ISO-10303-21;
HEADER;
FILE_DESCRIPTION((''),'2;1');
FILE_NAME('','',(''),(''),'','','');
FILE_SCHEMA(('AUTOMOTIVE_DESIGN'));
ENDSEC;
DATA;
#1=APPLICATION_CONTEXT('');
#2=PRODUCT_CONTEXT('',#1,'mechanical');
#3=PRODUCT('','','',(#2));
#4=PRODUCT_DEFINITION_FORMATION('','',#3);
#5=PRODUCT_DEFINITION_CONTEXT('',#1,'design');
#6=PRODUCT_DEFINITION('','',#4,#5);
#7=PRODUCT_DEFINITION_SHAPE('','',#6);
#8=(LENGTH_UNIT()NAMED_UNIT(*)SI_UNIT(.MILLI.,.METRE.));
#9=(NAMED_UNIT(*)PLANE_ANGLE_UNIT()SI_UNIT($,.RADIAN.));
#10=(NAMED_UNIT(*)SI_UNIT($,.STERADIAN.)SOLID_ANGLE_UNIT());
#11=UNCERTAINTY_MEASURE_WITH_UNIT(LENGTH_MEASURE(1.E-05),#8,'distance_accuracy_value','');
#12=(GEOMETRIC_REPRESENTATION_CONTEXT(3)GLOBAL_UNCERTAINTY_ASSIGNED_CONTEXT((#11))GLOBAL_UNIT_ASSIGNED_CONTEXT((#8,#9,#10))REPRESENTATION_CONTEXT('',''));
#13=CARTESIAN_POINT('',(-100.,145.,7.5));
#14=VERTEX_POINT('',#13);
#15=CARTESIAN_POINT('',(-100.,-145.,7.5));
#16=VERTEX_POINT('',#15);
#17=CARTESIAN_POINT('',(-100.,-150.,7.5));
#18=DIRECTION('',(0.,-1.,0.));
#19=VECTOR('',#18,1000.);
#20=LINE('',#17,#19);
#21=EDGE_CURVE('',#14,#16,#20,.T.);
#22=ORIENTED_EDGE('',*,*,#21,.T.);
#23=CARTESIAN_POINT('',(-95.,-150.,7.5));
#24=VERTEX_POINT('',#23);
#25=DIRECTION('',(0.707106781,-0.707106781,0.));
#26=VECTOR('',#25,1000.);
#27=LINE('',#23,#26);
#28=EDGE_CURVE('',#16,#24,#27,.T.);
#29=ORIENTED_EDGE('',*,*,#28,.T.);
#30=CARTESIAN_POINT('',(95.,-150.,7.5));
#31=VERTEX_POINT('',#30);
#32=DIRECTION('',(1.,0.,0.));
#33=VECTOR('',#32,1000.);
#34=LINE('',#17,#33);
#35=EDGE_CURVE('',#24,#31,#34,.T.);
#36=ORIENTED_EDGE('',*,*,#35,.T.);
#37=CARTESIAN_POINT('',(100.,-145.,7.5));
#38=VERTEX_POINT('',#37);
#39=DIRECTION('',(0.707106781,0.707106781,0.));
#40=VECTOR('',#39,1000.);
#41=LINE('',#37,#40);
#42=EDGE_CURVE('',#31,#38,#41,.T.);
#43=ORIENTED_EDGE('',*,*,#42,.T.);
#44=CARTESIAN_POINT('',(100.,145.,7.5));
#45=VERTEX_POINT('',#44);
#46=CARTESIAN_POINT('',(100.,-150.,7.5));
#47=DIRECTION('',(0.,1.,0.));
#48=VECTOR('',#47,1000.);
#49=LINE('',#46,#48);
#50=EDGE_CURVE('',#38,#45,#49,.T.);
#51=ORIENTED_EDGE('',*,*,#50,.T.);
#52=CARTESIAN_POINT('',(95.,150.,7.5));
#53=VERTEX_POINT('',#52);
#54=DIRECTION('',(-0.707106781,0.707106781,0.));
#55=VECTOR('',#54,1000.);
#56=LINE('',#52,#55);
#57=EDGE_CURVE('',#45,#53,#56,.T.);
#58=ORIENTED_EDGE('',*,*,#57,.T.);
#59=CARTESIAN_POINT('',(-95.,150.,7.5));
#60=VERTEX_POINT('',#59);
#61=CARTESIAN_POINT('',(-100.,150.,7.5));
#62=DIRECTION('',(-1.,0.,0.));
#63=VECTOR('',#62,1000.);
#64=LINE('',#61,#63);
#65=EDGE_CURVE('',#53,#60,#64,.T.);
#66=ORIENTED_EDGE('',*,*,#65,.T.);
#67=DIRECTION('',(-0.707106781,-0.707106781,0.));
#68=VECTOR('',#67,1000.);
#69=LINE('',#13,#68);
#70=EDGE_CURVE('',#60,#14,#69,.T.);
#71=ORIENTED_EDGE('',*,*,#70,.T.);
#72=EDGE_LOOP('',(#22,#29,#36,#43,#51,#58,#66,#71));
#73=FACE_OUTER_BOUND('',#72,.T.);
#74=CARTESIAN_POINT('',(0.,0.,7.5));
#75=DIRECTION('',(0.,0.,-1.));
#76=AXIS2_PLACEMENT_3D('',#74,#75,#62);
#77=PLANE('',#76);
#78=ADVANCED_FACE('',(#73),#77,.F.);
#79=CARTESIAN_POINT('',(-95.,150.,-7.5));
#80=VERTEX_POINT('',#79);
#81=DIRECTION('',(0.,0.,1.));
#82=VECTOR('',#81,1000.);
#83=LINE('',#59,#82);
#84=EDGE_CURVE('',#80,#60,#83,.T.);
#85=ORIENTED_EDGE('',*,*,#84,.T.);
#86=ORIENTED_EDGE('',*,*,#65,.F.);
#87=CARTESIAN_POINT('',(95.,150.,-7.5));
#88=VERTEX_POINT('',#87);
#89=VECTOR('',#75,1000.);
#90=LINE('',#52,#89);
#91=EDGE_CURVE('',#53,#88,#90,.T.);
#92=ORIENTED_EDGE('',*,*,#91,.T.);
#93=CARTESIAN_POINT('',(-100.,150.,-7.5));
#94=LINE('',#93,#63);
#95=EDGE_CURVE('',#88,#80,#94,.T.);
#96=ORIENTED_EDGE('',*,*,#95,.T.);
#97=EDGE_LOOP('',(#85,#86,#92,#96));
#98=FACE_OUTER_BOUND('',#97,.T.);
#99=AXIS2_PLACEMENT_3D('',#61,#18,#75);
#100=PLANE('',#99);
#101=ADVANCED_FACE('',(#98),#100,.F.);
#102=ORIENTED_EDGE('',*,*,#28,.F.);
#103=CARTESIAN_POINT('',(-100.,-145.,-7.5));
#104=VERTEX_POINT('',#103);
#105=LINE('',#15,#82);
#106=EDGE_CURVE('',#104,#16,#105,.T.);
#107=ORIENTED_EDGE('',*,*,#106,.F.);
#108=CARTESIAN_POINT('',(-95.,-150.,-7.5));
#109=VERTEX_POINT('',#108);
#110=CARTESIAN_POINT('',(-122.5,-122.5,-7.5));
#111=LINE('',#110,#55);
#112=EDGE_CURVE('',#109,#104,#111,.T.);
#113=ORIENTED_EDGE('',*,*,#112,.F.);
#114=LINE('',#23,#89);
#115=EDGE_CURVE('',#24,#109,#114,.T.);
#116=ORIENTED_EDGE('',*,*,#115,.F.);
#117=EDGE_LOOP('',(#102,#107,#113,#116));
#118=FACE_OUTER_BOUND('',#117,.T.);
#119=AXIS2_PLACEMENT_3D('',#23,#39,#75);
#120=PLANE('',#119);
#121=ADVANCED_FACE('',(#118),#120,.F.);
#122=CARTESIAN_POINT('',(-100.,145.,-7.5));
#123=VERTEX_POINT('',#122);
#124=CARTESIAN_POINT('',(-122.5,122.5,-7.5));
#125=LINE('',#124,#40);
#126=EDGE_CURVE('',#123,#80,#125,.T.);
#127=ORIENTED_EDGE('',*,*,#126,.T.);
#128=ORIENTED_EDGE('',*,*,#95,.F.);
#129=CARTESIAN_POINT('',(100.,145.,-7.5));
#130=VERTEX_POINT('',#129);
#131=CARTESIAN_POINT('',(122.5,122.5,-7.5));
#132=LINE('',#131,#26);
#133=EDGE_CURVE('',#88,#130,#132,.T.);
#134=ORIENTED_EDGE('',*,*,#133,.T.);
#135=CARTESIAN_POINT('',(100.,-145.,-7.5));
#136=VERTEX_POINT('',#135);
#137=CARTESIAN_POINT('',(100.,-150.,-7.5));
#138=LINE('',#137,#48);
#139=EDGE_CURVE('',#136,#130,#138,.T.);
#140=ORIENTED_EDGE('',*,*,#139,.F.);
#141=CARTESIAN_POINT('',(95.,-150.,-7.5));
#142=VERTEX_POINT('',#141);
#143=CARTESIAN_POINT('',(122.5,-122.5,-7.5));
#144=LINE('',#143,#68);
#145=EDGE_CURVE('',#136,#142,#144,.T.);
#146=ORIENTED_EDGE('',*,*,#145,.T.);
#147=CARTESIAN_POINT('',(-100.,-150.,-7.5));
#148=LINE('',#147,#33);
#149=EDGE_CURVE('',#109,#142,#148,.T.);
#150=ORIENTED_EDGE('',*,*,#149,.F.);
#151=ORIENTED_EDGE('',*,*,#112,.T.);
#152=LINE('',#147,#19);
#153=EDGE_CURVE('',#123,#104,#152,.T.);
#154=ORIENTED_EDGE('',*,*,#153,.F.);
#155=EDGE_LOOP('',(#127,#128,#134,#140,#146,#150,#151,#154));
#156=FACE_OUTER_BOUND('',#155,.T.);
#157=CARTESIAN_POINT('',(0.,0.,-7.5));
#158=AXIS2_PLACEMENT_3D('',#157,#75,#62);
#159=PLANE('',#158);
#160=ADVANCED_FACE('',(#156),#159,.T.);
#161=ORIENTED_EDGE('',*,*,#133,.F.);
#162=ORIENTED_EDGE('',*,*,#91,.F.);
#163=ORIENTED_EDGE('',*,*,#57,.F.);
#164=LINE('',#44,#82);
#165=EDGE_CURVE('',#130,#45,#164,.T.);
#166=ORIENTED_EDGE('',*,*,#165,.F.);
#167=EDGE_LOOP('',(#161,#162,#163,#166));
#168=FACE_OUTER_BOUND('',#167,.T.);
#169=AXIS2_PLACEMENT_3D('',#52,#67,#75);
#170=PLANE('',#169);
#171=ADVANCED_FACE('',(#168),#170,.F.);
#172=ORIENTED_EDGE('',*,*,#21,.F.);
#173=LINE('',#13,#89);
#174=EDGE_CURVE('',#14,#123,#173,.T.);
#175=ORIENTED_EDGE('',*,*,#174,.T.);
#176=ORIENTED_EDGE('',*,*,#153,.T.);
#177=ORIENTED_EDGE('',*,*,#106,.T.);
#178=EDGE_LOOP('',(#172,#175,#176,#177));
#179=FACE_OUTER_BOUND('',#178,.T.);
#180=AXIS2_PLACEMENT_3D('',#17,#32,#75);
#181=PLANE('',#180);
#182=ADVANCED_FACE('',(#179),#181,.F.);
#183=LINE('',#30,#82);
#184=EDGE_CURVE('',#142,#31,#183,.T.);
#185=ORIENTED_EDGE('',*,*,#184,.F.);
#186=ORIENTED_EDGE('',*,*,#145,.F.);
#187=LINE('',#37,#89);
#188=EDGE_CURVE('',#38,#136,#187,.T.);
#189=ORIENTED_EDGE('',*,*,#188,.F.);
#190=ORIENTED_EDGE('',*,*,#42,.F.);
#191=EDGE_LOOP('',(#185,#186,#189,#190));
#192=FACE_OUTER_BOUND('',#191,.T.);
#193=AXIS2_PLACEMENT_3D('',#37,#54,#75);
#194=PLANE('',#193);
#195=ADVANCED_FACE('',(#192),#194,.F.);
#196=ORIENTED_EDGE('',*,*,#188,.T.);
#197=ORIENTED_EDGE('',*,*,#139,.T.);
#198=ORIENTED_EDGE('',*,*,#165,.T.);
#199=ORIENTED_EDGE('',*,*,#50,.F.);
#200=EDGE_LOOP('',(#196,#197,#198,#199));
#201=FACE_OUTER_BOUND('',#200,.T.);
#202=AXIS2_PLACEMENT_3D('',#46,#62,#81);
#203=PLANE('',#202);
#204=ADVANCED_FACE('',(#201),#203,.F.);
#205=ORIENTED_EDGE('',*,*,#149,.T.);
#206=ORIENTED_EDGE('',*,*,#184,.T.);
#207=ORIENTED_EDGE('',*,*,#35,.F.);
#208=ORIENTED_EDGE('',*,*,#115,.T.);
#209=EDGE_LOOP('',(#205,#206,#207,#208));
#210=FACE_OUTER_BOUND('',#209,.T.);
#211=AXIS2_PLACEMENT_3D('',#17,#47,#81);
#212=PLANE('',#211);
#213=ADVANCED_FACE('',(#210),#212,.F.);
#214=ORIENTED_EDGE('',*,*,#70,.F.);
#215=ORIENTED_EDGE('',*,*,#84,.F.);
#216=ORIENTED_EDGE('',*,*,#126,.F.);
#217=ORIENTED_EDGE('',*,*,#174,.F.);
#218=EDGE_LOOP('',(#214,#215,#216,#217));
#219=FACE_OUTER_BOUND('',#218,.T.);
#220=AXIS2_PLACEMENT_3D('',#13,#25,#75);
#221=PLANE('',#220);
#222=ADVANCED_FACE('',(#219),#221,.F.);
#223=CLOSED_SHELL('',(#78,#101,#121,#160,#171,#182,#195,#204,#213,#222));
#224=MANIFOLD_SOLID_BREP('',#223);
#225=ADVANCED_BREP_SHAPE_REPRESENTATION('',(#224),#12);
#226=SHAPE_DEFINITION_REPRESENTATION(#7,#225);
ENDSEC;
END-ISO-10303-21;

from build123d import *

# Parameters (mm, degrees)
SKETCH_1_W      = 200
SKETCH_1_H      = 300
EXTRUDE_1_DEPTH = 7.5
CHAMFER_1_SIZE  = 5


with BuildPart() as part:
    # 草图1 → 凸台-拉伸1 (new, symmetric)
    with BuildSketch(Plane.XY):
        Rectangle(SKETCH_1_W, SKETCH_1_H)
    extrude(amount=EXTRUDE_1_DEPTH, both=True)

    # 倒角1
    chamfer_1_edges = [part.edges().sort_by_distance(p)[0] for p in [
        (100, -150, 0),
        (-100, -150, 0),
        (-100, 150, 0),
        (100, 150, 0),
    ]]
    chamfer(chamfer_1_edges, length=CHAMFER_1_SIZE)


solid = part.part
